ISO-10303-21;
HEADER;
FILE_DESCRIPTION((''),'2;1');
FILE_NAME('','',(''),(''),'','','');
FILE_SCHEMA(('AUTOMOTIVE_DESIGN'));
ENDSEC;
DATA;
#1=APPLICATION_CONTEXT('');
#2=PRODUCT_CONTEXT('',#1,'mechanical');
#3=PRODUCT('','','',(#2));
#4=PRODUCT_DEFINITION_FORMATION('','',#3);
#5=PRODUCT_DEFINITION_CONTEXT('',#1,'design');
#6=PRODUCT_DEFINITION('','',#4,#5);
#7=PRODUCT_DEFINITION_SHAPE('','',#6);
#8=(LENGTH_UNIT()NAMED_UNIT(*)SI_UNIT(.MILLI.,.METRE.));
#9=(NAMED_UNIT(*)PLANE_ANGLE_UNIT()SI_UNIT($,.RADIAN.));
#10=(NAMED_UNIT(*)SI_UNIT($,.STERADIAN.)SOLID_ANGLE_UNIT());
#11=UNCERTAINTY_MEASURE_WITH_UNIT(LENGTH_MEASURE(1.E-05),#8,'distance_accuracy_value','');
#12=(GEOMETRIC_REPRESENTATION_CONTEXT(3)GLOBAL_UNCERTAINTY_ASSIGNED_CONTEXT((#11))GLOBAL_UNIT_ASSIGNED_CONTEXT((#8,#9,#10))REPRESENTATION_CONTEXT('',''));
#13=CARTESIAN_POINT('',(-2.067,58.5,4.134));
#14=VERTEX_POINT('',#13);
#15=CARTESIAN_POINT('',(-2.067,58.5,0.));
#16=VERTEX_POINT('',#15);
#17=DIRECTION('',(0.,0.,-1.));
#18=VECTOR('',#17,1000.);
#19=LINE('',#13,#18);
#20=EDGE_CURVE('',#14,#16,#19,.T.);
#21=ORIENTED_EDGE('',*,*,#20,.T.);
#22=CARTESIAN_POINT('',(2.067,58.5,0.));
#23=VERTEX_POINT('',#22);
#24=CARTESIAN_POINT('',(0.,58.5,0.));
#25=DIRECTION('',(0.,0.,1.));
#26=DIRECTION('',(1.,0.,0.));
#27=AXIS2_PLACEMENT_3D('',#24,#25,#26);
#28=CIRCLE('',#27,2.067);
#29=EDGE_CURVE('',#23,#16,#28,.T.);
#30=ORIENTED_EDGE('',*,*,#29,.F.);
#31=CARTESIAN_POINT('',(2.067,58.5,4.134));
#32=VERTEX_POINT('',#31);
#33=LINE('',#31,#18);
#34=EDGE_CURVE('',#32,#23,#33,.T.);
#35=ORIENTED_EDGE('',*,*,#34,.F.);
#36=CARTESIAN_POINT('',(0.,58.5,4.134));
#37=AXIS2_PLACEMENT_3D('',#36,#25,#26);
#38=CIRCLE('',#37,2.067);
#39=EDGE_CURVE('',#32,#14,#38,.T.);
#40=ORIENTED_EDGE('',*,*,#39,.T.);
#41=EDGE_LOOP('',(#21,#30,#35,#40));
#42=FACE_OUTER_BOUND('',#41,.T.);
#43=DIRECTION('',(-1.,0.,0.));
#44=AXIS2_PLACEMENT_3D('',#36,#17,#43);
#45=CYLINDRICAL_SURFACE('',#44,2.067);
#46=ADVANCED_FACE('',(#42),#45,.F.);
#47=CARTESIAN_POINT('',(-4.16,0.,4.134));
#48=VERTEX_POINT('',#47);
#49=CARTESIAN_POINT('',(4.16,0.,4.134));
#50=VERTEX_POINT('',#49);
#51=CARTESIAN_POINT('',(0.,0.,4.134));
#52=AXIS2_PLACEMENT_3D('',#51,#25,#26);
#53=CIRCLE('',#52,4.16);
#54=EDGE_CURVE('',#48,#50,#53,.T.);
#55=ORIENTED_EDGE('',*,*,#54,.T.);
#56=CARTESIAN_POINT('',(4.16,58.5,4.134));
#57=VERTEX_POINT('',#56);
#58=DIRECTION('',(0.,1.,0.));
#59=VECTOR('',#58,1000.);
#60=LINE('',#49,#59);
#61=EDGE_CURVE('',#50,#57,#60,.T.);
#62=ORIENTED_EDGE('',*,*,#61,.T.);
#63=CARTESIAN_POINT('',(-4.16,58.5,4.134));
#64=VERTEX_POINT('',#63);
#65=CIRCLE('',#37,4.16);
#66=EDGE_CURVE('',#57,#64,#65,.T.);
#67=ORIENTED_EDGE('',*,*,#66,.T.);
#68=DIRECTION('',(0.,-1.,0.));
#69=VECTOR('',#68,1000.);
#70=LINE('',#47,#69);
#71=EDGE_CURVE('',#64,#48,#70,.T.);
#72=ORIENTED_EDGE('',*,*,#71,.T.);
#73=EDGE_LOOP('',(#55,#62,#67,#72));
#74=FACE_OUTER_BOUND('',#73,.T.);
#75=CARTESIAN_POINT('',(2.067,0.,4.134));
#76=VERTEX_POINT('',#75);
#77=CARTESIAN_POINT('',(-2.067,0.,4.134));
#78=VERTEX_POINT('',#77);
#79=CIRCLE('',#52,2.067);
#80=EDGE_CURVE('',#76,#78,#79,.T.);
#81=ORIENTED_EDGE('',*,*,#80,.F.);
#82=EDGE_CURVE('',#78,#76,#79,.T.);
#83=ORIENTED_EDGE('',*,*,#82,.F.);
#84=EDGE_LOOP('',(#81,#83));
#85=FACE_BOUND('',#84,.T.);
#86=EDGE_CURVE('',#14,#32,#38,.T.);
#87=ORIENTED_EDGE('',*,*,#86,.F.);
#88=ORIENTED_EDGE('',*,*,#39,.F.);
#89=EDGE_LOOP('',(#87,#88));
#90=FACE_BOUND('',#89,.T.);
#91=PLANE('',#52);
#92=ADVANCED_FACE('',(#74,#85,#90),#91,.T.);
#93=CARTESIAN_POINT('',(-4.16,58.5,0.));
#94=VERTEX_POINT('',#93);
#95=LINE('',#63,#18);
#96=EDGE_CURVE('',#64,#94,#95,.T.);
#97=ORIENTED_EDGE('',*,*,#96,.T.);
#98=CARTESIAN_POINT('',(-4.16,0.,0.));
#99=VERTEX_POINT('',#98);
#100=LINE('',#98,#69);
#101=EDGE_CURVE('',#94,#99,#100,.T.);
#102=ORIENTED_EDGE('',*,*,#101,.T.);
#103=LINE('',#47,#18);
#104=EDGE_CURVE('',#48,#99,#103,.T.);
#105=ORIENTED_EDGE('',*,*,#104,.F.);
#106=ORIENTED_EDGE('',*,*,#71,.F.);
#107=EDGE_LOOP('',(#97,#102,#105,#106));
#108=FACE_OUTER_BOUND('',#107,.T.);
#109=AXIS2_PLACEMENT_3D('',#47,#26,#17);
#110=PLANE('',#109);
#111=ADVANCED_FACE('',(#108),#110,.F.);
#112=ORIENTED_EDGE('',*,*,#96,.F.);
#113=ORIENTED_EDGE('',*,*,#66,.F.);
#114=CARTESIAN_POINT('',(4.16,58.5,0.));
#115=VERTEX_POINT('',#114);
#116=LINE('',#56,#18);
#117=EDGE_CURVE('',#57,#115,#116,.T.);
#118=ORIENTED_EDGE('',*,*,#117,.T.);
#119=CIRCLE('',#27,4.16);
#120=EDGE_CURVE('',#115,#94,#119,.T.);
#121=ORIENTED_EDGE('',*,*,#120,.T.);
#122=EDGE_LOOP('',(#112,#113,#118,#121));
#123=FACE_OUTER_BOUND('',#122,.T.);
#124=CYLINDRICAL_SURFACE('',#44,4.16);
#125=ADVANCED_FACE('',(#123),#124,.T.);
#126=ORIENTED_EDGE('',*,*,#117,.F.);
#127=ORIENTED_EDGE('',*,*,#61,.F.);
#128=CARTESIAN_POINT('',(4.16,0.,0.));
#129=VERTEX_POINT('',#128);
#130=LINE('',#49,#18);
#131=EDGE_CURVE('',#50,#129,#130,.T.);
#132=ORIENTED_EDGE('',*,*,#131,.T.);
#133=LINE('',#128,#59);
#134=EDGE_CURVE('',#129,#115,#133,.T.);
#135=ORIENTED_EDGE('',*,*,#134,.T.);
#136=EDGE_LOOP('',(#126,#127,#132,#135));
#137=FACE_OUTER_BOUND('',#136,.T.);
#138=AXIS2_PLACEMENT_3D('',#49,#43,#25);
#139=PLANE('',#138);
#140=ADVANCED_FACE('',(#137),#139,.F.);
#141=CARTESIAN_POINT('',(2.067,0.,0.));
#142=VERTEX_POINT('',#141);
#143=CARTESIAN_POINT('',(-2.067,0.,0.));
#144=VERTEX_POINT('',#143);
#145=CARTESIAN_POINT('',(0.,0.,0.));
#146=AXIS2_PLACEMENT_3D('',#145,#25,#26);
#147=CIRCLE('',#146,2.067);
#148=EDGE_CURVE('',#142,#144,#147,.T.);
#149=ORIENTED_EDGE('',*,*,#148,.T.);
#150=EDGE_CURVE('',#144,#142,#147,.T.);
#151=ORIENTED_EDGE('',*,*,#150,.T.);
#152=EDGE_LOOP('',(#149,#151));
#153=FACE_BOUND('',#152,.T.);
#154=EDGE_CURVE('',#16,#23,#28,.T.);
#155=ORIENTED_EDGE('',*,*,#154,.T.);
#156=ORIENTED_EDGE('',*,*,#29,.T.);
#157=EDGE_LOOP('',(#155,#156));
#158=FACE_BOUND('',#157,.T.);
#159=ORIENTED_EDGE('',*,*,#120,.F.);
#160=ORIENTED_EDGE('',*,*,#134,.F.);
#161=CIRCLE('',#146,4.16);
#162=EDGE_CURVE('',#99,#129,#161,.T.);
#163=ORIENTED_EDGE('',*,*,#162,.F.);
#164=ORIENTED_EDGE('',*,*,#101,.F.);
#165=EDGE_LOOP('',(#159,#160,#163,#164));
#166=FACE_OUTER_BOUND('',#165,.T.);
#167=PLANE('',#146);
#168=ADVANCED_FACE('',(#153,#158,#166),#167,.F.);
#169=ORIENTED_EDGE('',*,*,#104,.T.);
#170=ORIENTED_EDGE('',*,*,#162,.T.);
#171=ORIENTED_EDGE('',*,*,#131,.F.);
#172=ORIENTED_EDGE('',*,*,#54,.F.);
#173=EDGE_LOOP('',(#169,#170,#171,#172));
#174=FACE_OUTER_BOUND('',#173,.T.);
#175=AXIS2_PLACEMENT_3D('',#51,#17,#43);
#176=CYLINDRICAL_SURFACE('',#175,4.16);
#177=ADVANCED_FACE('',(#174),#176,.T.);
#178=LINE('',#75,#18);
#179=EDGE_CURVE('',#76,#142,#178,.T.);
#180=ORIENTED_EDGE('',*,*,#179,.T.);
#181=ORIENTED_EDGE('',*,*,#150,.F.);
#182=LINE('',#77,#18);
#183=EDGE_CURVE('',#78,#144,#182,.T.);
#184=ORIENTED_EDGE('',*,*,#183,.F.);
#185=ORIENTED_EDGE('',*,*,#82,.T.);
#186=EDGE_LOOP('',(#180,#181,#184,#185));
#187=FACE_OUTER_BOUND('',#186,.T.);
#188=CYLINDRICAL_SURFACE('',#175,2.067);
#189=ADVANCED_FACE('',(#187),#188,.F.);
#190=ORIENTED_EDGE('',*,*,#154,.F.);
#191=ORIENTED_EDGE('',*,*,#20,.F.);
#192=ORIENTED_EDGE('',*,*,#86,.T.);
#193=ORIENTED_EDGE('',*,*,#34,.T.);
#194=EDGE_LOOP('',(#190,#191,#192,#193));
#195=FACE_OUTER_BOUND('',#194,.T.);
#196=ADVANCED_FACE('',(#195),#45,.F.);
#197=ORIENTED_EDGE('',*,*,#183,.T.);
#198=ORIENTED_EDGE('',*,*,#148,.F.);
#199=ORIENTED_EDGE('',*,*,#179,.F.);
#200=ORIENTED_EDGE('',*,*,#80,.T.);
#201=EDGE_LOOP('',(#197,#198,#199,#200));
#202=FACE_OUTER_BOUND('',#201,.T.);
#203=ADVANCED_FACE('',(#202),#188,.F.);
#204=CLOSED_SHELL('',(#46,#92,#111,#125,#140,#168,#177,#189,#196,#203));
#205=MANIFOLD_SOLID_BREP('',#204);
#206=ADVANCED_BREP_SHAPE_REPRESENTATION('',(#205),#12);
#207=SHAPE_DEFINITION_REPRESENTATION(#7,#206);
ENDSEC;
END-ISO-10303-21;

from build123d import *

# Parameters (mm, degrees)
SKETCH1_R           = 1.59
BOSS_EXTRUDE1_DEPTH = 3.18
SCALE_RATIO_1_SCALE = 1.3


with BuildPart() as part:
    # Sketch1 → Boss-Extrude1 (new body)
    with BuildSketch(Plane.XY):
        with BuildLine():
            Line((-3.2, 0), (-3.2, 45))
            ThreePointArc((-3.2, 45), (0, 48.2), (3.2, 45))
            Line((3.2, 45), (3.2, 0))
            ThreePointArc((3.2, 0), (0, -3.2), (-3.2, 0))
        make_face()
        with Locations(Location((0, 0, 0), (0, 0, 180))):
            Circle(SKETCH1_R, mode=Mode.SUBTRACT)
        with Locations(Location((0, 45, 0), (0, 0, 180))):
            Circle(SKETCH1_R, mode=Mode.SUBTRACT)
    extrude(amount=BOSS_EXTRUDE1_DEPTH)


with BuildPart() as part_1:
    # Scale ratio 1: scaled about (0, 0, 0)
    add(part.part.scale(SCALE_RATIO_1_SCALE))


solid = part_1.part
